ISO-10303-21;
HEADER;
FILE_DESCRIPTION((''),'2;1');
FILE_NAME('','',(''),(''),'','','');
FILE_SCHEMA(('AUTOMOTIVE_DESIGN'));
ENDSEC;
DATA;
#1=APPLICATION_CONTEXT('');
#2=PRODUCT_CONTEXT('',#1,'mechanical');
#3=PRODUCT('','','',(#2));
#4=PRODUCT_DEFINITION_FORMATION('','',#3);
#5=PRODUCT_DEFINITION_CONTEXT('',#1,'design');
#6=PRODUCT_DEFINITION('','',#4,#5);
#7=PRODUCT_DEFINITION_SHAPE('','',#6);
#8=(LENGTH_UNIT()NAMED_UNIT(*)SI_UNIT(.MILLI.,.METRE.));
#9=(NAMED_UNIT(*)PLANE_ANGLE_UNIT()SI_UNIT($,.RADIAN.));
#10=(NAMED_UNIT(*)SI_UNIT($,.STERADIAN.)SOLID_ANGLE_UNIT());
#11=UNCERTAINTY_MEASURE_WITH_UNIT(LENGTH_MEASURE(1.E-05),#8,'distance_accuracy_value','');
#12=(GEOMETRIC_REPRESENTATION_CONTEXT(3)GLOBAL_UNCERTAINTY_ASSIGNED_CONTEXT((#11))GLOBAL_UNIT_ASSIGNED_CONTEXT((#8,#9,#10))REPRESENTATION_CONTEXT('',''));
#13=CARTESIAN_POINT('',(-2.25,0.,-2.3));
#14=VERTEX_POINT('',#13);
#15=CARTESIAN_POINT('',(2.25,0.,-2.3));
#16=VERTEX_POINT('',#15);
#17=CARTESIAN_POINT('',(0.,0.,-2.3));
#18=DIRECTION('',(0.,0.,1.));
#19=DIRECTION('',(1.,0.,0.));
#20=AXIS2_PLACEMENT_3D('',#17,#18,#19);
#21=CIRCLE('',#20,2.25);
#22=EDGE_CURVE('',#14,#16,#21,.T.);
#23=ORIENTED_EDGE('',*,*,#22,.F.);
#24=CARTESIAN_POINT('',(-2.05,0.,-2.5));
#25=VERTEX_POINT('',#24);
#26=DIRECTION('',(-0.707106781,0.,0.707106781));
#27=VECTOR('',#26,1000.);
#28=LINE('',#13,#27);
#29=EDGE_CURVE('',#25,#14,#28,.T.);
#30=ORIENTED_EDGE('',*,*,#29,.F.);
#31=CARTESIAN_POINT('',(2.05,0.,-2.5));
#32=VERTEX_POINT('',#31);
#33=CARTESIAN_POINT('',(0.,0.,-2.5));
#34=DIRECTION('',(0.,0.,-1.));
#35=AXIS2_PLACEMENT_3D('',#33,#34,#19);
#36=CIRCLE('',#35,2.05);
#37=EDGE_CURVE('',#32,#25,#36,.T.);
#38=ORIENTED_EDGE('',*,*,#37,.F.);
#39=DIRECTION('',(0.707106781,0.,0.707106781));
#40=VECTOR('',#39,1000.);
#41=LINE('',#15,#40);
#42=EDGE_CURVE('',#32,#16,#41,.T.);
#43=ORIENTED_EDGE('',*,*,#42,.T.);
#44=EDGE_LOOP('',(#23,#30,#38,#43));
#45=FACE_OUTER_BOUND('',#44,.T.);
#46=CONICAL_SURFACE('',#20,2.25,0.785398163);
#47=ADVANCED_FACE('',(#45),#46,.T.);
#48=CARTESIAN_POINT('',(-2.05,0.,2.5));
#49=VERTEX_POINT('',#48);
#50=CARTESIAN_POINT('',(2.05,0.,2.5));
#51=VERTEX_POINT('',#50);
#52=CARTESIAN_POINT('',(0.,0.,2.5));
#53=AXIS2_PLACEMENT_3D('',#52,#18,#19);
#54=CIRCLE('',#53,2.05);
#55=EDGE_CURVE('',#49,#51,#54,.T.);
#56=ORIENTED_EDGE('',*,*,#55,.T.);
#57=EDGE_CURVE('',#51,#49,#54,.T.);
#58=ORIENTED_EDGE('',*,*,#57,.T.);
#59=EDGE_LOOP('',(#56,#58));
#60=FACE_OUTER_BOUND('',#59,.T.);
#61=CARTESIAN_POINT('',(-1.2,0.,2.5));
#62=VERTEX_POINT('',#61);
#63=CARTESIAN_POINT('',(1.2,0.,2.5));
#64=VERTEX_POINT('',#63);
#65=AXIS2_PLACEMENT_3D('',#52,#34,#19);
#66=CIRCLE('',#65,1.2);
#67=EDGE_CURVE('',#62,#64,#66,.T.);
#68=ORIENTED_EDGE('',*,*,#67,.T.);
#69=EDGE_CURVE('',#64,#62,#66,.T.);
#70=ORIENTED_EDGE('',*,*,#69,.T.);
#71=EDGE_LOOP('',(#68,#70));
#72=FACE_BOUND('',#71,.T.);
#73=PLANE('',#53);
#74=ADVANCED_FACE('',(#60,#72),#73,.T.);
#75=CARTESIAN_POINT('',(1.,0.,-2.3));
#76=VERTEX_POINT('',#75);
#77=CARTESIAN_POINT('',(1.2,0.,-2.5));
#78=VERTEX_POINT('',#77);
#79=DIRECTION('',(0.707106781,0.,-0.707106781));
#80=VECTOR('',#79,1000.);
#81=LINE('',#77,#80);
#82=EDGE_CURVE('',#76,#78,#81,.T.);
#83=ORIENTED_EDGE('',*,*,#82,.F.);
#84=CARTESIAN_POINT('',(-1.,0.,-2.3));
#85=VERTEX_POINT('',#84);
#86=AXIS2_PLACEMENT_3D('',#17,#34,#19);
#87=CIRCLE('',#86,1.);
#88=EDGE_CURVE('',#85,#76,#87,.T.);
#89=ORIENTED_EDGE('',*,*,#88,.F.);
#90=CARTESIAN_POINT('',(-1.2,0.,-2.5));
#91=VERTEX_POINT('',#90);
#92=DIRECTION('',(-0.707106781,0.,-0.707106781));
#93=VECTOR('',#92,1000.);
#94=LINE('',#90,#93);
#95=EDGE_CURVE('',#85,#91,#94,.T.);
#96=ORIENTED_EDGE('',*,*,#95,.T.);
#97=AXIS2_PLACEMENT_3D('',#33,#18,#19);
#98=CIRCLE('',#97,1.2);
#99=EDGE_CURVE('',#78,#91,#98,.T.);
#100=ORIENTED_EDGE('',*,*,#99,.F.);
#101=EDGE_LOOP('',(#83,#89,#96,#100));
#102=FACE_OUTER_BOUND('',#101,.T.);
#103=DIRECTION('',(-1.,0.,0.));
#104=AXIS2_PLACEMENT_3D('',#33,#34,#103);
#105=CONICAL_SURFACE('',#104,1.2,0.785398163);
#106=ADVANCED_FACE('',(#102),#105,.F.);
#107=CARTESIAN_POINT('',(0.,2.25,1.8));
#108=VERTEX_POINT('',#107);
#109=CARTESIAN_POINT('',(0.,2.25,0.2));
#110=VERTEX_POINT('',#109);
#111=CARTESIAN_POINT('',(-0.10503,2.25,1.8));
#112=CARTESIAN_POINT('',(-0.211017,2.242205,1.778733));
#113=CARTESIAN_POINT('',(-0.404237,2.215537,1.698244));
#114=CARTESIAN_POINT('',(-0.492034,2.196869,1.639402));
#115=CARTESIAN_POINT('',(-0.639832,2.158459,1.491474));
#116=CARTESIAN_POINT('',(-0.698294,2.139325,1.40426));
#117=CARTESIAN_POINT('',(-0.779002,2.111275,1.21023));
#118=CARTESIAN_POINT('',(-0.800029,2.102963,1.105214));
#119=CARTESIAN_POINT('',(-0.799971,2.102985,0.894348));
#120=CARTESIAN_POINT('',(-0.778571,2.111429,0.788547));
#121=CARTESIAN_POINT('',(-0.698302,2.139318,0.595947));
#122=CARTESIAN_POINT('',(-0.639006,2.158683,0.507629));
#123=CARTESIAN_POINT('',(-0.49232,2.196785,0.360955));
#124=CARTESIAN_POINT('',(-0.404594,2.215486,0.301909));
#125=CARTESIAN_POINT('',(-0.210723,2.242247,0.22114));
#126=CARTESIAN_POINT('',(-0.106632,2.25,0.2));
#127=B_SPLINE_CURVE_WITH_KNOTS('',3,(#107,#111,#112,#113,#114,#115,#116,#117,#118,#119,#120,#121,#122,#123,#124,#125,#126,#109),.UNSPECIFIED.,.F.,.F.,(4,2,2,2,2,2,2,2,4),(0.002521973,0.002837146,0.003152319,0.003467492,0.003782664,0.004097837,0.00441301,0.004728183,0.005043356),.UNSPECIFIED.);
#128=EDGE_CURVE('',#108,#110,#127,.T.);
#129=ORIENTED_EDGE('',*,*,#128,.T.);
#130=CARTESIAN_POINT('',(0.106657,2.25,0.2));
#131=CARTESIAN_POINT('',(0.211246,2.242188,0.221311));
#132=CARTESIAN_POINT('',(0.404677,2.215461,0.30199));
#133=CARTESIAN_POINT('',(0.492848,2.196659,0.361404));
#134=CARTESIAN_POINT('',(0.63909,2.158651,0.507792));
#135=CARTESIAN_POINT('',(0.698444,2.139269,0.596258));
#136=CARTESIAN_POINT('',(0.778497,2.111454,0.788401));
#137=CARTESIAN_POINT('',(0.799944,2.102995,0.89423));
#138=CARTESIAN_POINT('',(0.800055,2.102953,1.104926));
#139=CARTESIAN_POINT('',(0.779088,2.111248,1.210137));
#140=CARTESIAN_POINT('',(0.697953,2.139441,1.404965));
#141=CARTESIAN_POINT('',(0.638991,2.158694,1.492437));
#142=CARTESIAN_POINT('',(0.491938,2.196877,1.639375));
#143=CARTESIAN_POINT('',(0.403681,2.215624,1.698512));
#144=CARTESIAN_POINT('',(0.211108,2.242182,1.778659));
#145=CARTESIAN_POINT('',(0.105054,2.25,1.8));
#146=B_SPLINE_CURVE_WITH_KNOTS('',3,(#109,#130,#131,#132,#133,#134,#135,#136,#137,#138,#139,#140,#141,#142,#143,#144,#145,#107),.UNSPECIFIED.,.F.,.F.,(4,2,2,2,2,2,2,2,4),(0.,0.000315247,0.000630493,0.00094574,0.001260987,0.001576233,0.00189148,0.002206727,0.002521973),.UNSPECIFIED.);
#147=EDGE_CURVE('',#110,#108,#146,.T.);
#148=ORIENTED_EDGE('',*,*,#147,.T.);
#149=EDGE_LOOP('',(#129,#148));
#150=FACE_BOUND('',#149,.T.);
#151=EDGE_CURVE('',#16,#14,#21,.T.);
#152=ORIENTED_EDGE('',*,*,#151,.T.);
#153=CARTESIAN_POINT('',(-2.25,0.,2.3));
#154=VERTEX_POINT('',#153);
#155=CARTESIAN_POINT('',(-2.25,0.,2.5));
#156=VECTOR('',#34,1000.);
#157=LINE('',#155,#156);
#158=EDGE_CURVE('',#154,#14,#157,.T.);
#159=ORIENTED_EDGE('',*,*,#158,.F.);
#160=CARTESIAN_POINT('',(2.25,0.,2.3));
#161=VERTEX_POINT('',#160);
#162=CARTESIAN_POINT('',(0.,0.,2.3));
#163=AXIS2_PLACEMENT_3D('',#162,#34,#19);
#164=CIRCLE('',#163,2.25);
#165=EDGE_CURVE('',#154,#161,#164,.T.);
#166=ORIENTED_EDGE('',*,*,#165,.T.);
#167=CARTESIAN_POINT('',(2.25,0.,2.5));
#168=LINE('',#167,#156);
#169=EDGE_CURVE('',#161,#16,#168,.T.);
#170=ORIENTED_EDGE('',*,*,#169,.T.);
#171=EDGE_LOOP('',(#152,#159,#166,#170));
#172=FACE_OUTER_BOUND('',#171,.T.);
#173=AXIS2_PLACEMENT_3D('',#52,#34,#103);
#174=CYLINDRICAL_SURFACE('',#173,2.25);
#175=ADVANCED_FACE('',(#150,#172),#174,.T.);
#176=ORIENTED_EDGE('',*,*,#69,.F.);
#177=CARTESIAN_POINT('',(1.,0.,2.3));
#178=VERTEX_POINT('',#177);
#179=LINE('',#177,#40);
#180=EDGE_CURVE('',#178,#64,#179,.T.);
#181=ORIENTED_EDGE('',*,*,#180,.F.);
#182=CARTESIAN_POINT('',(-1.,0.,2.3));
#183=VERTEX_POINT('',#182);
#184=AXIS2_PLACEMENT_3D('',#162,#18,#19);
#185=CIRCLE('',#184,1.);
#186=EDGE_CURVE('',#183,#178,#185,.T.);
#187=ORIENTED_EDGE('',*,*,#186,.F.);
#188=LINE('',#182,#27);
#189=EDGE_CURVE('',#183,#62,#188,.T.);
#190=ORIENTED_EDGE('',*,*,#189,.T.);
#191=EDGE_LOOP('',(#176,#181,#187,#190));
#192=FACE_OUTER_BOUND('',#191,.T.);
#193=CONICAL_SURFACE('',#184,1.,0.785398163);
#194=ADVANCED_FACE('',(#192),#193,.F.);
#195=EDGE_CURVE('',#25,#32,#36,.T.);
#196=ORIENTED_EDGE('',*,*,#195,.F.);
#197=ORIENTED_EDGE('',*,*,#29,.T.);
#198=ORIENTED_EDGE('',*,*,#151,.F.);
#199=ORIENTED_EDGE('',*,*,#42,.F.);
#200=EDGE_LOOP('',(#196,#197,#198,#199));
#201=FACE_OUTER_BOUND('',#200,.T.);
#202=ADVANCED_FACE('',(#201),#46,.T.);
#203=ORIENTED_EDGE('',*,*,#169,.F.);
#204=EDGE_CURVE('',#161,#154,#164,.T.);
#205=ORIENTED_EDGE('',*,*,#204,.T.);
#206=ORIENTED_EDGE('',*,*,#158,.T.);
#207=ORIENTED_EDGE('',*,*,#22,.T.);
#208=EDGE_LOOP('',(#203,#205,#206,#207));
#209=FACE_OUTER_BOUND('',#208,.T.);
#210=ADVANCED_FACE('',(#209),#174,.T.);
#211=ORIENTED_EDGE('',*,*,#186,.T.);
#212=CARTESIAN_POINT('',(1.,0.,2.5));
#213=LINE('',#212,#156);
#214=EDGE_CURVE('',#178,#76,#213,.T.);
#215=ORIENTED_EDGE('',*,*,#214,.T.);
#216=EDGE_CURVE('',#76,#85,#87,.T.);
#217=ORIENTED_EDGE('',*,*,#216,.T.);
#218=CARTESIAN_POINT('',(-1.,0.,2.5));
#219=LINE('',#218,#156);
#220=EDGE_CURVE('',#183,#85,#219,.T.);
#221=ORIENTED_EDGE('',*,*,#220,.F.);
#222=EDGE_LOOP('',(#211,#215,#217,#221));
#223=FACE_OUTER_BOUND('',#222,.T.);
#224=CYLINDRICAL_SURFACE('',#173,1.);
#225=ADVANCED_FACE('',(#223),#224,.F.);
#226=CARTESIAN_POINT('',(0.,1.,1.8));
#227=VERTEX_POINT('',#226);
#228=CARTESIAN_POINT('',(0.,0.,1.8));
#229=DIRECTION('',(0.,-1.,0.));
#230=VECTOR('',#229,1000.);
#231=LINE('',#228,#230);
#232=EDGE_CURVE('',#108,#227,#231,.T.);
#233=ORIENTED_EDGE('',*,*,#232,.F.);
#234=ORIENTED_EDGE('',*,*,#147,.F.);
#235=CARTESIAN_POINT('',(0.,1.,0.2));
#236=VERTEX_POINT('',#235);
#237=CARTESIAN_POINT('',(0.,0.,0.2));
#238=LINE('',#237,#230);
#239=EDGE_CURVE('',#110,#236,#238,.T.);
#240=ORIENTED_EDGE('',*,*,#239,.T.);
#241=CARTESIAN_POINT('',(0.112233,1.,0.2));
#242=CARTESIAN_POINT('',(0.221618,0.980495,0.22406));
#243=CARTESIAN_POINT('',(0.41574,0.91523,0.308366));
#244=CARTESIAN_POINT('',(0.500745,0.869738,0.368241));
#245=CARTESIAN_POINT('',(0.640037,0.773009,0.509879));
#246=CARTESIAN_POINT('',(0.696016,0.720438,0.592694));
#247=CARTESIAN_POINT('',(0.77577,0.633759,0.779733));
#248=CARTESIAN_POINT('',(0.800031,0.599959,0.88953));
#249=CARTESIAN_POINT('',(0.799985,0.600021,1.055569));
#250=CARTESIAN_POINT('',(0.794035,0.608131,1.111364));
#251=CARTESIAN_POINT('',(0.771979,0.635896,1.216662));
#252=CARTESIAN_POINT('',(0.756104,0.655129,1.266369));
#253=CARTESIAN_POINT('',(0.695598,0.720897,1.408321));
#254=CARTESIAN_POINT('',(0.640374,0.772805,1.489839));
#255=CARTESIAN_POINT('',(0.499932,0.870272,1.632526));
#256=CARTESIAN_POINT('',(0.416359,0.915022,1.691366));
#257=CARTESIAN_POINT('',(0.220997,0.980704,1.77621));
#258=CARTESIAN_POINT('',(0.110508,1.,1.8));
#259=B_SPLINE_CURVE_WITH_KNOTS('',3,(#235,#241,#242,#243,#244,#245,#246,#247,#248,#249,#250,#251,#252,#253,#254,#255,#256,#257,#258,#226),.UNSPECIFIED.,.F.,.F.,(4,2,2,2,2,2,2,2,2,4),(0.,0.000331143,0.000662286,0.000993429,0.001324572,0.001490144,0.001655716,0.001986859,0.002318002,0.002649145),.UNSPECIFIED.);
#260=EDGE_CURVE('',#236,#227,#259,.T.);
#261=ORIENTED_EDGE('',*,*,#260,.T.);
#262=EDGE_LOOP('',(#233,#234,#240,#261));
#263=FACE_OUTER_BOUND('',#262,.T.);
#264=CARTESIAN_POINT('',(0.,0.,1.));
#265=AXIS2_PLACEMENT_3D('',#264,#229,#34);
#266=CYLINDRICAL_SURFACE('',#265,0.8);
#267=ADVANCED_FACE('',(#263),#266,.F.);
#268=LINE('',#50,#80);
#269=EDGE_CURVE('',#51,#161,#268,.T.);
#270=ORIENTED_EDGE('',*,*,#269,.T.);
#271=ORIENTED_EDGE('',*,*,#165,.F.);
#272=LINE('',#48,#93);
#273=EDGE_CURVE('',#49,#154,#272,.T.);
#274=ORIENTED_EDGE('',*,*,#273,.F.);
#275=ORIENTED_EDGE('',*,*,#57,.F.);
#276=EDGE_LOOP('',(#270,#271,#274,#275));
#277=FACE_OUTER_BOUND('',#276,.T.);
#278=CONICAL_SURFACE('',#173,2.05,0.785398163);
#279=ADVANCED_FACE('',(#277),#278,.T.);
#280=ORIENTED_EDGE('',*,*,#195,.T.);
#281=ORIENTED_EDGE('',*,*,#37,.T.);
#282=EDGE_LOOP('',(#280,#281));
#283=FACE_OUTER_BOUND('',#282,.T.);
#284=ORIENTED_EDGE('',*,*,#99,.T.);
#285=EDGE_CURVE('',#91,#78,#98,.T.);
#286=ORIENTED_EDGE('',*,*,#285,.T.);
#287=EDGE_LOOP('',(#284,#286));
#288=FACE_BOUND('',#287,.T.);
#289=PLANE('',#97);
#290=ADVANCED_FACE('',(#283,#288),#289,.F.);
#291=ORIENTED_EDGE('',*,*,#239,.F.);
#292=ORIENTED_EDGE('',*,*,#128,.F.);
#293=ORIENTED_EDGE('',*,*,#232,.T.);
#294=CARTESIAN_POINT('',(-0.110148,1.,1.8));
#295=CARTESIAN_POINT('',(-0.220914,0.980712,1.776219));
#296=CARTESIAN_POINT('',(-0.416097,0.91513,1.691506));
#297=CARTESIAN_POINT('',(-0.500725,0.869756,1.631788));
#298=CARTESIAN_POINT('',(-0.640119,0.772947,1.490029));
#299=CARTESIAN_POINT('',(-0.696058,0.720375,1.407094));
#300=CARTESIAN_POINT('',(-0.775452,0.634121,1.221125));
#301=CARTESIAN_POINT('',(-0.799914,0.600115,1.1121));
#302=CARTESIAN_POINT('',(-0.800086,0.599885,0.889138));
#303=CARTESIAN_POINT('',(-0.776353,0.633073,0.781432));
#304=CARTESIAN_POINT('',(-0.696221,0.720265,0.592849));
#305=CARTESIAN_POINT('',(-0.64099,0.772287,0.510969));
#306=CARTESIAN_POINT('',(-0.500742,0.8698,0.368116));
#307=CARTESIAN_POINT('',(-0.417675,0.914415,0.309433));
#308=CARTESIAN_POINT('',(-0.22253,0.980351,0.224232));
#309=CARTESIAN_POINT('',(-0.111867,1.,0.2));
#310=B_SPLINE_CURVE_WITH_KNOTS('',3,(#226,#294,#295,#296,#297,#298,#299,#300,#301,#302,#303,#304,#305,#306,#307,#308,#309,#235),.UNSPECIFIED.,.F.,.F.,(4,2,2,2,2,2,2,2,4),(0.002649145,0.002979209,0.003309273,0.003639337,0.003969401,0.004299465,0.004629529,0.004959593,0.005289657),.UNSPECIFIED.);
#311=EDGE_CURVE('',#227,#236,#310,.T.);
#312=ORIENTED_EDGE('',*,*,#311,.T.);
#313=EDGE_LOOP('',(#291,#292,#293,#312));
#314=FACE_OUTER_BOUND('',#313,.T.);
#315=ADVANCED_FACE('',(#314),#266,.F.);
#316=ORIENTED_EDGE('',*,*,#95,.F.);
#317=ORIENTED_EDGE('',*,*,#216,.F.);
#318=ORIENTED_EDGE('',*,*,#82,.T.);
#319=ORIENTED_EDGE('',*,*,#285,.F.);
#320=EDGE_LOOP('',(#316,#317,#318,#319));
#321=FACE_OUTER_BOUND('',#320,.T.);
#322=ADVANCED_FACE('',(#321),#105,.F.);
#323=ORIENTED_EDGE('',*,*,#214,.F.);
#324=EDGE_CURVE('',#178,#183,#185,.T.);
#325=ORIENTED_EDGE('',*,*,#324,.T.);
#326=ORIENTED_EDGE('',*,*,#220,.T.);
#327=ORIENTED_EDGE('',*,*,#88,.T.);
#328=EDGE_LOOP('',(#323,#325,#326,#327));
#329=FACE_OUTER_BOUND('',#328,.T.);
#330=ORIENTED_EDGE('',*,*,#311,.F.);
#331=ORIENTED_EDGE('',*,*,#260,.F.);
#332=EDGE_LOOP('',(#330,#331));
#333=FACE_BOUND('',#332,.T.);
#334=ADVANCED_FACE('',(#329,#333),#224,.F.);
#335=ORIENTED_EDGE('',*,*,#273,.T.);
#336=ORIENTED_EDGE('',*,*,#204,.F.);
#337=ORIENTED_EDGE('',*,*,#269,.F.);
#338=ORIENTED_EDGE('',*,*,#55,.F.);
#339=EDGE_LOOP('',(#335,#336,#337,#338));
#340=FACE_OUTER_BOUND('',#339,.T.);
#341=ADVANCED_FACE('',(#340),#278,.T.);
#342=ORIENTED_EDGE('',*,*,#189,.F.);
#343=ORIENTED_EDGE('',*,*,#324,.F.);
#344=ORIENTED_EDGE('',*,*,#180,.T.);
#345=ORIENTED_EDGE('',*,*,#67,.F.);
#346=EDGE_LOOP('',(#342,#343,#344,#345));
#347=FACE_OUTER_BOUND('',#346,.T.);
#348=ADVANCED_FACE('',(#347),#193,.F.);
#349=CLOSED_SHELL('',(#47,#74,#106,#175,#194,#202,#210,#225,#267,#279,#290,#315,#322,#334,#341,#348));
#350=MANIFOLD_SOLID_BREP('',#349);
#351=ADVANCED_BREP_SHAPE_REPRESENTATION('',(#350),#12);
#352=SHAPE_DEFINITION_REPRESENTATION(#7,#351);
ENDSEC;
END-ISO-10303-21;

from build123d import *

# Parameters (mm, degrees)
SKETCH1_R           = 2.25
SKETCH1_R_2         = 1
BOSS_EXTRUDE1_DEPTH = 2.5
CHAMFER1_SIZE       = 0.2
SKETCH2_W           = 0.8
SKETCH2_H           = 2.25


with BuildPart() as part:
    # Sketch1 → Boss-Extrude1 (new, symmetric)
    with BuildSketch(Plane.XY):
        Circle(SKETCH1_R)
        Circle(SKETCH1_R_2, mode=Mode.SUBTRACT)
    extrude(amount=BOSS_EXTRUDE1_DEPTH, both=True)

    # Chamfer1
    chamfer1_edges = [part.edges().sort_by_distance(p)[0] for p in [
        (-2.25, 0, -2.5),
        (-2.25, 0, 2.5),
        (-1, 0, -2.5),
        (-1, 0, 2.5),
    ]]
    chamfer(chamfer1_edges, length=CHAMFER1_SIZE)

    # Sketch2 → M2 Tapped Hole1 (revolve, cut)
    with BuildSketch(Plane(origin=(0, 0, 1), x_dir=(0, 0, -1), z_dir=(1, 0, 0))):
        with Locations((0.4, 1.125)):
            Rectangle(SKETCH2_W, SKETCH2_H)
    revolve(axis=Axis((0, -6.35, 1), (0, 1, 0)), mode=Mode.SUBTRACT)


solid = part.part
